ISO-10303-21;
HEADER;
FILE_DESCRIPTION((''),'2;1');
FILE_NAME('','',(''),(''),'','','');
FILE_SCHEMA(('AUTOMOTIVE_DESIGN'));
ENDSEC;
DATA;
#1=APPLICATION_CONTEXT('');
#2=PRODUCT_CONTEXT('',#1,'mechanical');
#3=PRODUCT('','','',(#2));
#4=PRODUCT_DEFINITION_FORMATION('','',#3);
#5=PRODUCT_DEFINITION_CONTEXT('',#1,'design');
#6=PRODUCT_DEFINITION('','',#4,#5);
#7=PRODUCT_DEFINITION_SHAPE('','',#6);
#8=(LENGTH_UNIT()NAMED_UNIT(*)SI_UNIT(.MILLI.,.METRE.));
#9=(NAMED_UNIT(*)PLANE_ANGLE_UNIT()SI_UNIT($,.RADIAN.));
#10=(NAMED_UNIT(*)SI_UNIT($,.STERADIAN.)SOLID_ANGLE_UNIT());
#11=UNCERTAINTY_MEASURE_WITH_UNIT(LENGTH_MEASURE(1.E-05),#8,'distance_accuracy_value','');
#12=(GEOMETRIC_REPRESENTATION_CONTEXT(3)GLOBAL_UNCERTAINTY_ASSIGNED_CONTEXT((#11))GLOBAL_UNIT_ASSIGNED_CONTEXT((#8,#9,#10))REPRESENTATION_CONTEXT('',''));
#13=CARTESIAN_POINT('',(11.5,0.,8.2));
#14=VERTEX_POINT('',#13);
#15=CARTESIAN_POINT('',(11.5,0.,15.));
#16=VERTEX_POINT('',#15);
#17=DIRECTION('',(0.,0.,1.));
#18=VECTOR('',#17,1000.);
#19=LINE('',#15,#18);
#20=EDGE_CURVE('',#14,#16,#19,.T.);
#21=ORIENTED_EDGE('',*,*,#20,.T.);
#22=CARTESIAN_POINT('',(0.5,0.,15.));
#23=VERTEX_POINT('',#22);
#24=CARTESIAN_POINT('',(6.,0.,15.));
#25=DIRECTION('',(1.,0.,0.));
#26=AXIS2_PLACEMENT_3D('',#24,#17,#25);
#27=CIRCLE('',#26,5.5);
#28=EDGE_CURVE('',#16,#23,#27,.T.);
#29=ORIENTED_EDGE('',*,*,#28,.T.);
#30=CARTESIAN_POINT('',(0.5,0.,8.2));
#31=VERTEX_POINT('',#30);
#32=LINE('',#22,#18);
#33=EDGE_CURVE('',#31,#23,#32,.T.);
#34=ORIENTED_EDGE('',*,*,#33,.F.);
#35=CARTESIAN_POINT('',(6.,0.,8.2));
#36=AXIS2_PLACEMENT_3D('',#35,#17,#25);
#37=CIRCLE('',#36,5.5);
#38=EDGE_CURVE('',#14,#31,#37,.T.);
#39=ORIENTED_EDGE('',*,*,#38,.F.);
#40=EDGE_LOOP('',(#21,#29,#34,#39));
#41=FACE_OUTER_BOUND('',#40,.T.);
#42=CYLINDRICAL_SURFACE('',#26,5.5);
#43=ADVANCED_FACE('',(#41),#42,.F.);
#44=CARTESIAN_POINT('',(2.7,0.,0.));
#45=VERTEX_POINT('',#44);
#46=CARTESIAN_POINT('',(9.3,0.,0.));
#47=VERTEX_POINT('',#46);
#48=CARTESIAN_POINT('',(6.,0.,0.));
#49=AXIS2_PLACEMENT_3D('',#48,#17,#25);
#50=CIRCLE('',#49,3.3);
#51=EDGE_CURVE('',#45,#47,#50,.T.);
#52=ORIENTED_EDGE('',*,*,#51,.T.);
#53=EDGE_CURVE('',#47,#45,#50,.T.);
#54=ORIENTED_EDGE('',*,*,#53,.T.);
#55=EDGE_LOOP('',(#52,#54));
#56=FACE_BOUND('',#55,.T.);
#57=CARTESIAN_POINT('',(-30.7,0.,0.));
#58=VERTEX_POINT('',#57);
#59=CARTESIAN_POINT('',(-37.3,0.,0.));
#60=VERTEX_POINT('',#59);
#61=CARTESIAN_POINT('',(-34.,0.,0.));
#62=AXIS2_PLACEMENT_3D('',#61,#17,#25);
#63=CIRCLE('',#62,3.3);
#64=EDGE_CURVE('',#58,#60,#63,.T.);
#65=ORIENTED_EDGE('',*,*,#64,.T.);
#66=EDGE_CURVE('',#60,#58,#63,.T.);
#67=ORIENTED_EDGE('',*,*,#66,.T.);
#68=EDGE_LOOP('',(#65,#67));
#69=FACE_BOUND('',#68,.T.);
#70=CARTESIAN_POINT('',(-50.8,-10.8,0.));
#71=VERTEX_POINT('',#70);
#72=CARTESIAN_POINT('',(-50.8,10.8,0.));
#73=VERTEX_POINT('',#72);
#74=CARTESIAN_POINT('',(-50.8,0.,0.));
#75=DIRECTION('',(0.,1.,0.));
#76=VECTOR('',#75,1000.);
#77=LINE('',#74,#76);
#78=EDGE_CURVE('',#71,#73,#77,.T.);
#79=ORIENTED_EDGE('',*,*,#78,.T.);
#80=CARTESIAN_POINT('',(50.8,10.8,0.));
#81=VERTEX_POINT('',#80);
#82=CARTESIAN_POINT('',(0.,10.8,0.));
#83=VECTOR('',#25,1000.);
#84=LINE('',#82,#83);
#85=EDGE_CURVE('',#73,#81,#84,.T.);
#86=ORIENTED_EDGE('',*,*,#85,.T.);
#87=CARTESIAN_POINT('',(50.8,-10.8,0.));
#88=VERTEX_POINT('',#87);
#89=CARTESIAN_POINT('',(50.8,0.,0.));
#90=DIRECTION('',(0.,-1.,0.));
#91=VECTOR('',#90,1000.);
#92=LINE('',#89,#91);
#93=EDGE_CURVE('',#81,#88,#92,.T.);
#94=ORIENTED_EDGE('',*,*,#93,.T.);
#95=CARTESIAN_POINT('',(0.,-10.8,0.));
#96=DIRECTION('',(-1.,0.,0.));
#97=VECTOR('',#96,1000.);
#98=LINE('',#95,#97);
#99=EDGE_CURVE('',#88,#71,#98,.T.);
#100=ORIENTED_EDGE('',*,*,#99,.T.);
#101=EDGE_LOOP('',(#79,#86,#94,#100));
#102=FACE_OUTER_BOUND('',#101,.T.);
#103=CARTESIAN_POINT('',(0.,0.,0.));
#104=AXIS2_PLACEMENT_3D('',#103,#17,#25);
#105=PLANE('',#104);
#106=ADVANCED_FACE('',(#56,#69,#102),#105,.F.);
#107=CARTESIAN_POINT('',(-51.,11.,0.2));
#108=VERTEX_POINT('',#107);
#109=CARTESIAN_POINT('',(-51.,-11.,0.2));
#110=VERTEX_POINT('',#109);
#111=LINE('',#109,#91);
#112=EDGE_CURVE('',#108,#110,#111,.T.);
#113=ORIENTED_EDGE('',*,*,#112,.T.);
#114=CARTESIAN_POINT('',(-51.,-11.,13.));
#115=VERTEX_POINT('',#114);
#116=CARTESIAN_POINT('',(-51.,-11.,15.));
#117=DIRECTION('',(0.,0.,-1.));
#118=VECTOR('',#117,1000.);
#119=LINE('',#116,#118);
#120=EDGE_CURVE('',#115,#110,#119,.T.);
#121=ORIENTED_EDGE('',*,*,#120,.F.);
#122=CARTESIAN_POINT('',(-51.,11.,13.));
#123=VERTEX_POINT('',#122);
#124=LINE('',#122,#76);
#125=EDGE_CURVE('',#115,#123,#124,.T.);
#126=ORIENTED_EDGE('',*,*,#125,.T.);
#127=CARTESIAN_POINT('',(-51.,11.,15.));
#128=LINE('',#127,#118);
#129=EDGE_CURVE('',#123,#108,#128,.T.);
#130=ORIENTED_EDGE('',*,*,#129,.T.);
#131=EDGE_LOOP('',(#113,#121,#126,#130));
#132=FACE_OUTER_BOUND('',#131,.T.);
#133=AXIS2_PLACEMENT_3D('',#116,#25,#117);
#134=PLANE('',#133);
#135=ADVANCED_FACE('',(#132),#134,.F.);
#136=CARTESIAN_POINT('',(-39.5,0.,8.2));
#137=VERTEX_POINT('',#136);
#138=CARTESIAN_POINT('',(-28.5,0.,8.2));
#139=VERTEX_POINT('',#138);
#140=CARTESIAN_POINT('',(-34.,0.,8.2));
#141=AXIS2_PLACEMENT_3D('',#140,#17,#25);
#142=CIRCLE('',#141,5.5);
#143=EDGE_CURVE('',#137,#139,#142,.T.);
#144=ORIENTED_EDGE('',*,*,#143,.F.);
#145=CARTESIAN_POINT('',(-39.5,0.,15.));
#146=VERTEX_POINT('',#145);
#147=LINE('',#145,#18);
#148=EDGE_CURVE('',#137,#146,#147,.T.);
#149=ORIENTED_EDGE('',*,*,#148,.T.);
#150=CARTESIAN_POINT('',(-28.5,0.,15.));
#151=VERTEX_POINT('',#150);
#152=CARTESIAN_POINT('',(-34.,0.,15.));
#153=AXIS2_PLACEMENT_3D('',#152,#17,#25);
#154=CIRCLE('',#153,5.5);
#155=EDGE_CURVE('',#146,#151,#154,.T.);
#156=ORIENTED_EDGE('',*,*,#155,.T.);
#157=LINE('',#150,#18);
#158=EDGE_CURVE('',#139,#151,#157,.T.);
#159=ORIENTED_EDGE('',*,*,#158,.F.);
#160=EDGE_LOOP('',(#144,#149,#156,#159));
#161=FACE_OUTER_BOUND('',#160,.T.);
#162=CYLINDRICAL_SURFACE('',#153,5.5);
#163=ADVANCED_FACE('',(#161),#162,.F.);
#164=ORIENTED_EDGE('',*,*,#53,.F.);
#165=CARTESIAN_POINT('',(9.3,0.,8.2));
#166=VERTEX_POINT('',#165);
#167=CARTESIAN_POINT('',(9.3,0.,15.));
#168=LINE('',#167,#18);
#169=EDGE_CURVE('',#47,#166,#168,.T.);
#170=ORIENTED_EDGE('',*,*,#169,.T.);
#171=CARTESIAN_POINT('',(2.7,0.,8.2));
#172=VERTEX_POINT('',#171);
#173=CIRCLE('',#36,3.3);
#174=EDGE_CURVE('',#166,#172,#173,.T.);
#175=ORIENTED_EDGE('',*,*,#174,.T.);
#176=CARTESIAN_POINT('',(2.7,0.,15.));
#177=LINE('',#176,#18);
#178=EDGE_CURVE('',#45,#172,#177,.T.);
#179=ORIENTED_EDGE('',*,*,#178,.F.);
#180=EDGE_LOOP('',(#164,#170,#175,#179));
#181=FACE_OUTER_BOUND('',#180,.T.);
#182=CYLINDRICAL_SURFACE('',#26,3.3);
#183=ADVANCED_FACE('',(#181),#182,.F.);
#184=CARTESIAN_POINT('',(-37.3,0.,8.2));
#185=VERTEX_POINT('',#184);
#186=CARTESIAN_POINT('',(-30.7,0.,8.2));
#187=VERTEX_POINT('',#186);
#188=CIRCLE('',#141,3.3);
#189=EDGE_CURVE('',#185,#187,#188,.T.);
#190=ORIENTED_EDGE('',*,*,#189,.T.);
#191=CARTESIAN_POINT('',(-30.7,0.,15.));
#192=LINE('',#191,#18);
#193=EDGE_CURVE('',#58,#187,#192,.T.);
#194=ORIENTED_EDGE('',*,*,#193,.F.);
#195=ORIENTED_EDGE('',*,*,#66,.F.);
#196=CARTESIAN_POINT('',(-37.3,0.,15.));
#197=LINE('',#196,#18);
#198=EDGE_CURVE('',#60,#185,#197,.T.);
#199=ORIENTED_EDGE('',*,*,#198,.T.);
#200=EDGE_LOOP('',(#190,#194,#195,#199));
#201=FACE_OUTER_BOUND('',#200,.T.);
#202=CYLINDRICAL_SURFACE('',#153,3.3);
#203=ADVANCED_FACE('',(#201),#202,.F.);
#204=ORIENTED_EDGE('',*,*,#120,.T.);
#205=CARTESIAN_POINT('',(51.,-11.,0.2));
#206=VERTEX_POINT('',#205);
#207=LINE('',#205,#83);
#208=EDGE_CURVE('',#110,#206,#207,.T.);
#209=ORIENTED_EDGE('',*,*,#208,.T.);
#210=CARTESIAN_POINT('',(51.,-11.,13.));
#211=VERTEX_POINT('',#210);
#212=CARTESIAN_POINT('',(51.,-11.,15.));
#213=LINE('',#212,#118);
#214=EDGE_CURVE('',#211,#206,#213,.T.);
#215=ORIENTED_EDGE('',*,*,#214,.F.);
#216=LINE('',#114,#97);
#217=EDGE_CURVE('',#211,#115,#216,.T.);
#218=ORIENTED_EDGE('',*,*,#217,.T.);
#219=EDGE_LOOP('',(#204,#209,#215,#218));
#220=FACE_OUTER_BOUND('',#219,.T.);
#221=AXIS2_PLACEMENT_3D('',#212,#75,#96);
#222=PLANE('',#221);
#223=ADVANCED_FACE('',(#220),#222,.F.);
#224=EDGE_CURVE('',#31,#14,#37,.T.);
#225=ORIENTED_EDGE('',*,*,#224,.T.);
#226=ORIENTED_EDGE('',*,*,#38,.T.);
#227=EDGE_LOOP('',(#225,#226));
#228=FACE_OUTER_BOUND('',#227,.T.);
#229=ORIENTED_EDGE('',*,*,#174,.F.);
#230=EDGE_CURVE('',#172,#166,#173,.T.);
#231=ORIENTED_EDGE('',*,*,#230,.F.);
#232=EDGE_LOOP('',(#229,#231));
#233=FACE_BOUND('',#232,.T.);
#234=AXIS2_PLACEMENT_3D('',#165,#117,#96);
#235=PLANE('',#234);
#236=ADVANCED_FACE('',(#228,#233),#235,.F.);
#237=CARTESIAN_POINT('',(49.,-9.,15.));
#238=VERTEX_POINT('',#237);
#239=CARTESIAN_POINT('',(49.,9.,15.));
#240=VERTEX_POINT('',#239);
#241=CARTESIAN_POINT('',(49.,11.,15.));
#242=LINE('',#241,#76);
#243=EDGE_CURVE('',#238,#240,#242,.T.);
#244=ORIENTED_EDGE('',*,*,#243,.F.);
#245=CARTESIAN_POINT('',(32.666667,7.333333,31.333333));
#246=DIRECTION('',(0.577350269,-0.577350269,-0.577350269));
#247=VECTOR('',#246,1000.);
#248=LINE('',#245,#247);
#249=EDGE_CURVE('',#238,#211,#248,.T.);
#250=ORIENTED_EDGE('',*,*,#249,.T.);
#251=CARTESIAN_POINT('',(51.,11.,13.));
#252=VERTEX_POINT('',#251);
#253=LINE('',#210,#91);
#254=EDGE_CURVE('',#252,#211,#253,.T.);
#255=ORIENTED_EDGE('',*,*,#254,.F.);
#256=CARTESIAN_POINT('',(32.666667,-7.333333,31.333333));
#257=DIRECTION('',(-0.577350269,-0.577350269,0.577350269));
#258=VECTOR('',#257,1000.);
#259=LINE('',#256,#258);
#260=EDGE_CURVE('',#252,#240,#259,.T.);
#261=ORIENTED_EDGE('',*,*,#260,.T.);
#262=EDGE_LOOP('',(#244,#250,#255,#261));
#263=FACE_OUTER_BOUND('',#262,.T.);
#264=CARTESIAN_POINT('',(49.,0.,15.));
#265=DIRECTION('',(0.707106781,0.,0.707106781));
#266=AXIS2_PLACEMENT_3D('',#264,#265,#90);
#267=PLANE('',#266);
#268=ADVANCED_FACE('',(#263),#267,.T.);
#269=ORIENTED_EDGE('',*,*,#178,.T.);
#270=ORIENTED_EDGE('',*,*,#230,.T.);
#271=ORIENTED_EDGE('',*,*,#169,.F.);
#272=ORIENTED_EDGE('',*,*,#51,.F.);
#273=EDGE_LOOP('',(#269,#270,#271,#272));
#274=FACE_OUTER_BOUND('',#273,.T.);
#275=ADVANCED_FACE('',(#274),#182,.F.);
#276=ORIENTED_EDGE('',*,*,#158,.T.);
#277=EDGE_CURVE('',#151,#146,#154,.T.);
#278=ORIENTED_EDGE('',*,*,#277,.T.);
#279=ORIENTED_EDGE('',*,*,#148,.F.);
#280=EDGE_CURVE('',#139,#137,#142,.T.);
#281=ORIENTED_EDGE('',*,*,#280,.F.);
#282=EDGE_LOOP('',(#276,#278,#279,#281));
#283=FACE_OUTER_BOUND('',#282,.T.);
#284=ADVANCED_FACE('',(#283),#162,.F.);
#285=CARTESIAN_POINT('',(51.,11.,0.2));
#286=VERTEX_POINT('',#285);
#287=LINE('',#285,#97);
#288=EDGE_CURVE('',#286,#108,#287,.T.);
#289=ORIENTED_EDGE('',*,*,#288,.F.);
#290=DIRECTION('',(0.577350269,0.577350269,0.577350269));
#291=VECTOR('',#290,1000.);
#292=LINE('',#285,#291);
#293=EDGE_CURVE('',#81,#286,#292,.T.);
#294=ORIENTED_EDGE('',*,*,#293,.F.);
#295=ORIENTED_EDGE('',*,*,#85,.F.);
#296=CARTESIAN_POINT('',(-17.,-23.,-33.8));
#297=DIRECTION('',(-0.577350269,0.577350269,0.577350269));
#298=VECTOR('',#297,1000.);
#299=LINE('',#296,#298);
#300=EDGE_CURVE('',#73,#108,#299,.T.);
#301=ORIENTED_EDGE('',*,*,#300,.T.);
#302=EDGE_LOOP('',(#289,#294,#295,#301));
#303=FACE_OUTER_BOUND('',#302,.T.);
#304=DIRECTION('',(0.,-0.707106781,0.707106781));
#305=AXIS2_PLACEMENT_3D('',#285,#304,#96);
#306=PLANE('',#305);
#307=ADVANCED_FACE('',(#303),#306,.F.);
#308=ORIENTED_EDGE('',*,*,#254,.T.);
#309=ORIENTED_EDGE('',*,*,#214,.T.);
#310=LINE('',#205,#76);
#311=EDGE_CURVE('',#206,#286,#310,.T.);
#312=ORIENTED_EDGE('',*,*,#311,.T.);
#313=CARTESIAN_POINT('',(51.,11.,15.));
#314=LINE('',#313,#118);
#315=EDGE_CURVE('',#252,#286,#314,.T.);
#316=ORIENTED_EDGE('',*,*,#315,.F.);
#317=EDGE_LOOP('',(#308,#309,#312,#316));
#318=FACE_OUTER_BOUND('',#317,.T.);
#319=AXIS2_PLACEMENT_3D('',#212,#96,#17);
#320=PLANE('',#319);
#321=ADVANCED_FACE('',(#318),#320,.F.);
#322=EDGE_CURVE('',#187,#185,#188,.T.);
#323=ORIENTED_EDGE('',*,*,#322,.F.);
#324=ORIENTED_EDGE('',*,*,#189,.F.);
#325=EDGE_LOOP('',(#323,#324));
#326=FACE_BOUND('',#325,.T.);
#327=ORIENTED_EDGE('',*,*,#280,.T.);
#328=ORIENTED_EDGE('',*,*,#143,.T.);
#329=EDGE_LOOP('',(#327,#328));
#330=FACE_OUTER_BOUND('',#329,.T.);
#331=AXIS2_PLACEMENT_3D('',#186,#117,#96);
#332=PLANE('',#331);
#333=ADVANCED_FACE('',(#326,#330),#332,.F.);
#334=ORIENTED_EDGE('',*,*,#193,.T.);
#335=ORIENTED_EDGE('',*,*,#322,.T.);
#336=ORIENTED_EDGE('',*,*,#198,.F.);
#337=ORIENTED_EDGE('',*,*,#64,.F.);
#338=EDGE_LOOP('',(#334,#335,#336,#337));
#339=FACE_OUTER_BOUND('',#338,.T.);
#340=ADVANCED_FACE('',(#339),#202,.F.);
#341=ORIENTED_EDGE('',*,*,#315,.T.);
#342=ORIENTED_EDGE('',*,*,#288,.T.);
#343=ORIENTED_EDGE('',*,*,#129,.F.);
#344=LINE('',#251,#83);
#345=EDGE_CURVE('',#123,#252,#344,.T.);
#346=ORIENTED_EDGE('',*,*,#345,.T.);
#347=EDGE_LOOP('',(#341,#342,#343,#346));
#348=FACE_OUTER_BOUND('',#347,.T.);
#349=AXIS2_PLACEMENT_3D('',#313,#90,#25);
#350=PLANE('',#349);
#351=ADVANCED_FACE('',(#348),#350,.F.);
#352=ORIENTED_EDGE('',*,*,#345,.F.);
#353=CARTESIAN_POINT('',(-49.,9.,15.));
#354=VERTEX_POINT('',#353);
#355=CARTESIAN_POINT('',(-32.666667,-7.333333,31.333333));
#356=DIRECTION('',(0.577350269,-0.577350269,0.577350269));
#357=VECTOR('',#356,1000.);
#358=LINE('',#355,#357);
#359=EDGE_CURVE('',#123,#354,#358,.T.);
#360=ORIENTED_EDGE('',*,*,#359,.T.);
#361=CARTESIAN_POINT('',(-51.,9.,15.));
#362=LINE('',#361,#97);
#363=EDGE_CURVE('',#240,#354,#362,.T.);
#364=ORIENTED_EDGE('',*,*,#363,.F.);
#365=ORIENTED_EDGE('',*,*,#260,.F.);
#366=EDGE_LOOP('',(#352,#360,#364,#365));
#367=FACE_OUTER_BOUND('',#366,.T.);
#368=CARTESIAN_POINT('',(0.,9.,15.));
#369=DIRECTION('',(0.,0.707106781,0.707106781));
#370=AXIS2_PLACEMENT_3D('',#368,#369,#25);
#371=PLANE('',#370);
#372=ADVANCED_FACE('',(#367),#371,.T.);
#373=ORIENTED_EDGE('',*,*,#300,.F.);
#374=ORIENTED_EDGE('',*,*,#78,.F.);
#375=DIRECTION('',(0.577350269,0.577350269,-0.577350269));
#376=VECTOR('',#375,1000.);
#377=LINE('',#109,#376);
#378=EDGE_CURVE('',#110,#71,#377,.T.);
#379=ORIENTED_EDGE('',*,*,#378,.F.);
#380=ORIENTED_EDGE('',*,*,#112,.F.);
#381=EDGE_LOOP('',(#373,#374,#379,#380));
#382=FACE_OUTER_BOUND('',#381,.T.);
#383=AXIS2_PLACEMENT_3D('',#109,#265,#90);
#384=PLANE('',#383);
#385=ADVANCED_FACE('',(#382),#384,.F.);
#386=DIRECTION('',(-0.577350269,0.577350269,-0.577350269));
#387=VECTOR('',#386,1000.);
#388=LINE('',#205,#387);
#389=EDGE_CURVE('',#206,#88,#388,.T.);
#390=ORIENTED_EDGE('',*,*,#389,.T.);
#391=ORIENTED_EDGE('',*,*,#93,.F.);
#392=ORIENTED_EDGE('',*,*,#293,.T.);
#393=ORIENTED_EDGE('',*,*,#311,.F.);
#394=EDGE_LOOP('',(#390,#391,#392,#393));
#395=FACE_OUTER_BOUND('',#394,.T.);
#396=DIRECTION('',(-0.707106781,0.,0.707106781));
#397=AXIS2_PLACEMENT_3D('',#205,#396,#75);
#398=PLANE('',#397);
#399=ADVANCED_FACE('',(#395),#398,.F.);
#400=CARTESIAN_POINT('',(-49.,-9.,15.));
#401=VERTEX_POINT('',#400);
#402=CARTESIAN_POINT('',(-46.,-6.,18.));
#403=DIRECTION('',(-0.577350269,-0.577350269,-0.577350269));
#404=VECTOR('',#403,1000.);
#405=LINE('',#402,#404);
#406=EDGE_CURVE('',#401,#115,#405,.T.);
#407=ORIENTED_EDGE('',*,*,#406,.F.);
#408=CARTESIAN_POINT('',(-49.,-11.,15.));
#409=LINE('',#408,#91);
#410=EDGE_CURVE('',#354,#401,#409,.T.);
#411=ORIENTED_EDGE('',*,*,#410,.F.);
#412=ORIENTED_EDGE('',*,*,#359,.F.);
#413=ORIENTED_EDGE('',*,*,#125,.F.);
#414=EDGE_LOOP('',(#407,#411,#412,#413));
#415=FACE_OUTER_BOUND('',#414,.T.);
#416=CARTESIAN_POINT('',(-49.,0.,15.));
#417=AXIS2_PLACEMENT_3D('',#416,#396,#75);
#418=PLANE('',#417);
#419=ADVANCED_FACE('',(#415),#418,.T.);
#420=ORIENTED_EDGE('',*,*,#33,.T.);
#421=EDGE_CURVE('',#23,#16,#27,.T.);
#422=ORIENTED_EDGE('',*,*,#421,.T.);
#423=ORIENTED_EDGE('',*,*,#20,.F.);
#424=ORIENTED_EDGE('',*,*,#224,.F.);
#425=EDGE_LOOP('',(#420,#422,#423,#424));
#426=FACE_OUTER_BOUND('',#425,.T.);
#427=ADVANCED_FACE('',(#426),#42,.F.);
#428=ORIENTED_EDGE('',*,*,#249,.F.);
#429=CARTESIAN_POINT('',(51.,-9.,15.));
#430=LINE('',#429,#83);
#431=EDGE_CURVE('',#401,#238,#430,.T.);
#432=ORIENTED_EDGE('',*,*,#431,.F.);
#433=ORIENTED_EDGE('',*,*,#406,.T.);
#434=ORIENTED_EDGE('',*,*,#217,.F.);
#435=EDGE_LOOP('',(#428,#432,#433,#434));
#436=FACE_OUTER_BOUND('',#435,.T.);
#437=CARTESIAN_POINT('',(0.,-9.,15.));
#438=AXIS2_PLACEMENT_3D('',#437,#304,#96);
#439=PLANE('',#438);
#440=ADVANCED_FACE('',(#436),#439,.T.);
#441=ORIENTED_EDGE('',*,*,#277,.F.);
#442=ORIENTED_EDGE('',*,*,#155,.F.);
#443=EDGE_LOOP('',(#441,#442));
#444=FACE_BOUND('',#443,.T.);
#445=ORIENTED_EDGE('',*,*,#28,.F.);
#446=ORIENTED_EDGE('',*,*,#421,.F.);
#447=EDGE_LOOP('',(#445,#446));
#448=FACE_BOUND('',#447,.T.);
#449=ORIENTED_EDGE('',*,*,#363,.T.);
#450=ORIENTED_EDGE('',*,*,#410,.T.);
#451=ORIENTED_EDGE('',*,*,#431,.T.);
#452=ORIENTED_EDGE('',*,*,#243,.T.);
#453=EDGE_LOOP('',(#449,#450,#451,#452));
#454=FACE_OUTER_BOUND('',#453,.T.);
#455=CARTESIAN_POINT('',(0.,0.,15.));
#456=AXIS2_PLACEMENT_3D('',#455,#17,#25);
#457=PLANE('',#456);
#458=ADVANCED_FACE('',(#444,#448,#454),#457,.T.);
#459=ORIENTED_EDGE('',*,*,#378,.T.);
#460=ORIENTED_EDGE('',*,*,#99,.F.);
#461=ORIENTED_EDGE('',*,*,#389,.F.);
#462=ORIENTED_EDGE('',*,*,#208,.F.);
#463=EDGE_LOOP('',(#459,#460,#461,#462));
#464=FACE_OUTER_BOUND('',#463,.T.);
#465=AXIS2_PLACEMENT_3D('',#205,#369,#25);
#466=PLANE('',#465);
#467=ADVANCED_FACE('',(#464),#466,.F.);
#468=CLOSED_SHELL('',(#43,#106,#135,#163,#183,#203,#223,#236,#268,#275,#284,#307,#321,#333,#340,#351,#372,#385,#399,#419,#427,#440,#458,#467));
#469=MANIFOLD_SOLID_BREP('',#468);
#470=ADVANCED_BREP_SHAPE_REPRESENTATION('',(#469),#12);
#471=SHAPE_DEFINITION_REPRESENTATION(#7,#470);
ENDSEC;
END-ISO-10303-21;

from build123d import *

# Parameters (mm, degrees)
SKETCH1_W                                            = 102
SKETCH1_H                                            = 22
BOSS_EXTRUDE1_DEPTH                                  = 15
HOLE_SIZE_PER_SOCKET_HEAD_CAP_SCREW_TYPE_D           = 6.6
HOLE_SIZE_PER_SOCKET_HEAD_CAP_SCREW_TYPE_CBORE_D     = 11
HOLE_SIZE_PER_SOCKET_HEAD_CAP_SCREW_TYPE_CBORE_DEPTH = 6.8
CHAMFER1_SIZE                                        = 0.2
CHAMFER2_SIZE                                        = 2


with BuildPart() as part:
    # Sketch1 → Boss-Extrude1 (new body)
    with BuildSketch(Plane.XY):
        Rectangle(SKETCH1_W, SKETCH1_H)
    extrude(amount=BOSS_EXTRUDE1_DEPTH)

    # Hole size per socket head cap screw type1 (through all)
    with Locations(Plane(origin=(-34, 0, 15), x_dir=(1, 0, 0), z_dir=(0, 0, 1))):
        with Locations((0, 0), (40, 0)):
            CounterBoreHole(HOLE_SIZE_PER_SOCKET_HEAD_CAP_SCREW_TYPE_D / 2, HOLE_SIZE_PER_SOCKET_HEAD_CAP_SCREW_TYPE_CBORE_D / 2, HOLE_SIZE_PER_SOCKET_HEAD_CAP_SCREW_TYPE_CBORE_DEPTH)

    # Chamfer1
    chamfer1_edges = [part.edges().sort_by_distance(p)[0] for p in [
        (0, 11, 0),
        (51, 0, 0),
        (0, -11, 0),
        (-51, 0, 0),
    ]]
    chamfer(chamfer1_edges, length=CHAMFER1_SIZE)

    # Chamfer2
    chamfer2_edges = [part.edges().sort_by_distance(p)[0] for p in [
        (51, 0, 15),
        (0, 11, 15),
        (-51, 0, 15),
        (0, -11, 15),
    ]]
    chamfer(chamfer2_edges, length=CHAMFER2_SIZE)


solid = part.part
